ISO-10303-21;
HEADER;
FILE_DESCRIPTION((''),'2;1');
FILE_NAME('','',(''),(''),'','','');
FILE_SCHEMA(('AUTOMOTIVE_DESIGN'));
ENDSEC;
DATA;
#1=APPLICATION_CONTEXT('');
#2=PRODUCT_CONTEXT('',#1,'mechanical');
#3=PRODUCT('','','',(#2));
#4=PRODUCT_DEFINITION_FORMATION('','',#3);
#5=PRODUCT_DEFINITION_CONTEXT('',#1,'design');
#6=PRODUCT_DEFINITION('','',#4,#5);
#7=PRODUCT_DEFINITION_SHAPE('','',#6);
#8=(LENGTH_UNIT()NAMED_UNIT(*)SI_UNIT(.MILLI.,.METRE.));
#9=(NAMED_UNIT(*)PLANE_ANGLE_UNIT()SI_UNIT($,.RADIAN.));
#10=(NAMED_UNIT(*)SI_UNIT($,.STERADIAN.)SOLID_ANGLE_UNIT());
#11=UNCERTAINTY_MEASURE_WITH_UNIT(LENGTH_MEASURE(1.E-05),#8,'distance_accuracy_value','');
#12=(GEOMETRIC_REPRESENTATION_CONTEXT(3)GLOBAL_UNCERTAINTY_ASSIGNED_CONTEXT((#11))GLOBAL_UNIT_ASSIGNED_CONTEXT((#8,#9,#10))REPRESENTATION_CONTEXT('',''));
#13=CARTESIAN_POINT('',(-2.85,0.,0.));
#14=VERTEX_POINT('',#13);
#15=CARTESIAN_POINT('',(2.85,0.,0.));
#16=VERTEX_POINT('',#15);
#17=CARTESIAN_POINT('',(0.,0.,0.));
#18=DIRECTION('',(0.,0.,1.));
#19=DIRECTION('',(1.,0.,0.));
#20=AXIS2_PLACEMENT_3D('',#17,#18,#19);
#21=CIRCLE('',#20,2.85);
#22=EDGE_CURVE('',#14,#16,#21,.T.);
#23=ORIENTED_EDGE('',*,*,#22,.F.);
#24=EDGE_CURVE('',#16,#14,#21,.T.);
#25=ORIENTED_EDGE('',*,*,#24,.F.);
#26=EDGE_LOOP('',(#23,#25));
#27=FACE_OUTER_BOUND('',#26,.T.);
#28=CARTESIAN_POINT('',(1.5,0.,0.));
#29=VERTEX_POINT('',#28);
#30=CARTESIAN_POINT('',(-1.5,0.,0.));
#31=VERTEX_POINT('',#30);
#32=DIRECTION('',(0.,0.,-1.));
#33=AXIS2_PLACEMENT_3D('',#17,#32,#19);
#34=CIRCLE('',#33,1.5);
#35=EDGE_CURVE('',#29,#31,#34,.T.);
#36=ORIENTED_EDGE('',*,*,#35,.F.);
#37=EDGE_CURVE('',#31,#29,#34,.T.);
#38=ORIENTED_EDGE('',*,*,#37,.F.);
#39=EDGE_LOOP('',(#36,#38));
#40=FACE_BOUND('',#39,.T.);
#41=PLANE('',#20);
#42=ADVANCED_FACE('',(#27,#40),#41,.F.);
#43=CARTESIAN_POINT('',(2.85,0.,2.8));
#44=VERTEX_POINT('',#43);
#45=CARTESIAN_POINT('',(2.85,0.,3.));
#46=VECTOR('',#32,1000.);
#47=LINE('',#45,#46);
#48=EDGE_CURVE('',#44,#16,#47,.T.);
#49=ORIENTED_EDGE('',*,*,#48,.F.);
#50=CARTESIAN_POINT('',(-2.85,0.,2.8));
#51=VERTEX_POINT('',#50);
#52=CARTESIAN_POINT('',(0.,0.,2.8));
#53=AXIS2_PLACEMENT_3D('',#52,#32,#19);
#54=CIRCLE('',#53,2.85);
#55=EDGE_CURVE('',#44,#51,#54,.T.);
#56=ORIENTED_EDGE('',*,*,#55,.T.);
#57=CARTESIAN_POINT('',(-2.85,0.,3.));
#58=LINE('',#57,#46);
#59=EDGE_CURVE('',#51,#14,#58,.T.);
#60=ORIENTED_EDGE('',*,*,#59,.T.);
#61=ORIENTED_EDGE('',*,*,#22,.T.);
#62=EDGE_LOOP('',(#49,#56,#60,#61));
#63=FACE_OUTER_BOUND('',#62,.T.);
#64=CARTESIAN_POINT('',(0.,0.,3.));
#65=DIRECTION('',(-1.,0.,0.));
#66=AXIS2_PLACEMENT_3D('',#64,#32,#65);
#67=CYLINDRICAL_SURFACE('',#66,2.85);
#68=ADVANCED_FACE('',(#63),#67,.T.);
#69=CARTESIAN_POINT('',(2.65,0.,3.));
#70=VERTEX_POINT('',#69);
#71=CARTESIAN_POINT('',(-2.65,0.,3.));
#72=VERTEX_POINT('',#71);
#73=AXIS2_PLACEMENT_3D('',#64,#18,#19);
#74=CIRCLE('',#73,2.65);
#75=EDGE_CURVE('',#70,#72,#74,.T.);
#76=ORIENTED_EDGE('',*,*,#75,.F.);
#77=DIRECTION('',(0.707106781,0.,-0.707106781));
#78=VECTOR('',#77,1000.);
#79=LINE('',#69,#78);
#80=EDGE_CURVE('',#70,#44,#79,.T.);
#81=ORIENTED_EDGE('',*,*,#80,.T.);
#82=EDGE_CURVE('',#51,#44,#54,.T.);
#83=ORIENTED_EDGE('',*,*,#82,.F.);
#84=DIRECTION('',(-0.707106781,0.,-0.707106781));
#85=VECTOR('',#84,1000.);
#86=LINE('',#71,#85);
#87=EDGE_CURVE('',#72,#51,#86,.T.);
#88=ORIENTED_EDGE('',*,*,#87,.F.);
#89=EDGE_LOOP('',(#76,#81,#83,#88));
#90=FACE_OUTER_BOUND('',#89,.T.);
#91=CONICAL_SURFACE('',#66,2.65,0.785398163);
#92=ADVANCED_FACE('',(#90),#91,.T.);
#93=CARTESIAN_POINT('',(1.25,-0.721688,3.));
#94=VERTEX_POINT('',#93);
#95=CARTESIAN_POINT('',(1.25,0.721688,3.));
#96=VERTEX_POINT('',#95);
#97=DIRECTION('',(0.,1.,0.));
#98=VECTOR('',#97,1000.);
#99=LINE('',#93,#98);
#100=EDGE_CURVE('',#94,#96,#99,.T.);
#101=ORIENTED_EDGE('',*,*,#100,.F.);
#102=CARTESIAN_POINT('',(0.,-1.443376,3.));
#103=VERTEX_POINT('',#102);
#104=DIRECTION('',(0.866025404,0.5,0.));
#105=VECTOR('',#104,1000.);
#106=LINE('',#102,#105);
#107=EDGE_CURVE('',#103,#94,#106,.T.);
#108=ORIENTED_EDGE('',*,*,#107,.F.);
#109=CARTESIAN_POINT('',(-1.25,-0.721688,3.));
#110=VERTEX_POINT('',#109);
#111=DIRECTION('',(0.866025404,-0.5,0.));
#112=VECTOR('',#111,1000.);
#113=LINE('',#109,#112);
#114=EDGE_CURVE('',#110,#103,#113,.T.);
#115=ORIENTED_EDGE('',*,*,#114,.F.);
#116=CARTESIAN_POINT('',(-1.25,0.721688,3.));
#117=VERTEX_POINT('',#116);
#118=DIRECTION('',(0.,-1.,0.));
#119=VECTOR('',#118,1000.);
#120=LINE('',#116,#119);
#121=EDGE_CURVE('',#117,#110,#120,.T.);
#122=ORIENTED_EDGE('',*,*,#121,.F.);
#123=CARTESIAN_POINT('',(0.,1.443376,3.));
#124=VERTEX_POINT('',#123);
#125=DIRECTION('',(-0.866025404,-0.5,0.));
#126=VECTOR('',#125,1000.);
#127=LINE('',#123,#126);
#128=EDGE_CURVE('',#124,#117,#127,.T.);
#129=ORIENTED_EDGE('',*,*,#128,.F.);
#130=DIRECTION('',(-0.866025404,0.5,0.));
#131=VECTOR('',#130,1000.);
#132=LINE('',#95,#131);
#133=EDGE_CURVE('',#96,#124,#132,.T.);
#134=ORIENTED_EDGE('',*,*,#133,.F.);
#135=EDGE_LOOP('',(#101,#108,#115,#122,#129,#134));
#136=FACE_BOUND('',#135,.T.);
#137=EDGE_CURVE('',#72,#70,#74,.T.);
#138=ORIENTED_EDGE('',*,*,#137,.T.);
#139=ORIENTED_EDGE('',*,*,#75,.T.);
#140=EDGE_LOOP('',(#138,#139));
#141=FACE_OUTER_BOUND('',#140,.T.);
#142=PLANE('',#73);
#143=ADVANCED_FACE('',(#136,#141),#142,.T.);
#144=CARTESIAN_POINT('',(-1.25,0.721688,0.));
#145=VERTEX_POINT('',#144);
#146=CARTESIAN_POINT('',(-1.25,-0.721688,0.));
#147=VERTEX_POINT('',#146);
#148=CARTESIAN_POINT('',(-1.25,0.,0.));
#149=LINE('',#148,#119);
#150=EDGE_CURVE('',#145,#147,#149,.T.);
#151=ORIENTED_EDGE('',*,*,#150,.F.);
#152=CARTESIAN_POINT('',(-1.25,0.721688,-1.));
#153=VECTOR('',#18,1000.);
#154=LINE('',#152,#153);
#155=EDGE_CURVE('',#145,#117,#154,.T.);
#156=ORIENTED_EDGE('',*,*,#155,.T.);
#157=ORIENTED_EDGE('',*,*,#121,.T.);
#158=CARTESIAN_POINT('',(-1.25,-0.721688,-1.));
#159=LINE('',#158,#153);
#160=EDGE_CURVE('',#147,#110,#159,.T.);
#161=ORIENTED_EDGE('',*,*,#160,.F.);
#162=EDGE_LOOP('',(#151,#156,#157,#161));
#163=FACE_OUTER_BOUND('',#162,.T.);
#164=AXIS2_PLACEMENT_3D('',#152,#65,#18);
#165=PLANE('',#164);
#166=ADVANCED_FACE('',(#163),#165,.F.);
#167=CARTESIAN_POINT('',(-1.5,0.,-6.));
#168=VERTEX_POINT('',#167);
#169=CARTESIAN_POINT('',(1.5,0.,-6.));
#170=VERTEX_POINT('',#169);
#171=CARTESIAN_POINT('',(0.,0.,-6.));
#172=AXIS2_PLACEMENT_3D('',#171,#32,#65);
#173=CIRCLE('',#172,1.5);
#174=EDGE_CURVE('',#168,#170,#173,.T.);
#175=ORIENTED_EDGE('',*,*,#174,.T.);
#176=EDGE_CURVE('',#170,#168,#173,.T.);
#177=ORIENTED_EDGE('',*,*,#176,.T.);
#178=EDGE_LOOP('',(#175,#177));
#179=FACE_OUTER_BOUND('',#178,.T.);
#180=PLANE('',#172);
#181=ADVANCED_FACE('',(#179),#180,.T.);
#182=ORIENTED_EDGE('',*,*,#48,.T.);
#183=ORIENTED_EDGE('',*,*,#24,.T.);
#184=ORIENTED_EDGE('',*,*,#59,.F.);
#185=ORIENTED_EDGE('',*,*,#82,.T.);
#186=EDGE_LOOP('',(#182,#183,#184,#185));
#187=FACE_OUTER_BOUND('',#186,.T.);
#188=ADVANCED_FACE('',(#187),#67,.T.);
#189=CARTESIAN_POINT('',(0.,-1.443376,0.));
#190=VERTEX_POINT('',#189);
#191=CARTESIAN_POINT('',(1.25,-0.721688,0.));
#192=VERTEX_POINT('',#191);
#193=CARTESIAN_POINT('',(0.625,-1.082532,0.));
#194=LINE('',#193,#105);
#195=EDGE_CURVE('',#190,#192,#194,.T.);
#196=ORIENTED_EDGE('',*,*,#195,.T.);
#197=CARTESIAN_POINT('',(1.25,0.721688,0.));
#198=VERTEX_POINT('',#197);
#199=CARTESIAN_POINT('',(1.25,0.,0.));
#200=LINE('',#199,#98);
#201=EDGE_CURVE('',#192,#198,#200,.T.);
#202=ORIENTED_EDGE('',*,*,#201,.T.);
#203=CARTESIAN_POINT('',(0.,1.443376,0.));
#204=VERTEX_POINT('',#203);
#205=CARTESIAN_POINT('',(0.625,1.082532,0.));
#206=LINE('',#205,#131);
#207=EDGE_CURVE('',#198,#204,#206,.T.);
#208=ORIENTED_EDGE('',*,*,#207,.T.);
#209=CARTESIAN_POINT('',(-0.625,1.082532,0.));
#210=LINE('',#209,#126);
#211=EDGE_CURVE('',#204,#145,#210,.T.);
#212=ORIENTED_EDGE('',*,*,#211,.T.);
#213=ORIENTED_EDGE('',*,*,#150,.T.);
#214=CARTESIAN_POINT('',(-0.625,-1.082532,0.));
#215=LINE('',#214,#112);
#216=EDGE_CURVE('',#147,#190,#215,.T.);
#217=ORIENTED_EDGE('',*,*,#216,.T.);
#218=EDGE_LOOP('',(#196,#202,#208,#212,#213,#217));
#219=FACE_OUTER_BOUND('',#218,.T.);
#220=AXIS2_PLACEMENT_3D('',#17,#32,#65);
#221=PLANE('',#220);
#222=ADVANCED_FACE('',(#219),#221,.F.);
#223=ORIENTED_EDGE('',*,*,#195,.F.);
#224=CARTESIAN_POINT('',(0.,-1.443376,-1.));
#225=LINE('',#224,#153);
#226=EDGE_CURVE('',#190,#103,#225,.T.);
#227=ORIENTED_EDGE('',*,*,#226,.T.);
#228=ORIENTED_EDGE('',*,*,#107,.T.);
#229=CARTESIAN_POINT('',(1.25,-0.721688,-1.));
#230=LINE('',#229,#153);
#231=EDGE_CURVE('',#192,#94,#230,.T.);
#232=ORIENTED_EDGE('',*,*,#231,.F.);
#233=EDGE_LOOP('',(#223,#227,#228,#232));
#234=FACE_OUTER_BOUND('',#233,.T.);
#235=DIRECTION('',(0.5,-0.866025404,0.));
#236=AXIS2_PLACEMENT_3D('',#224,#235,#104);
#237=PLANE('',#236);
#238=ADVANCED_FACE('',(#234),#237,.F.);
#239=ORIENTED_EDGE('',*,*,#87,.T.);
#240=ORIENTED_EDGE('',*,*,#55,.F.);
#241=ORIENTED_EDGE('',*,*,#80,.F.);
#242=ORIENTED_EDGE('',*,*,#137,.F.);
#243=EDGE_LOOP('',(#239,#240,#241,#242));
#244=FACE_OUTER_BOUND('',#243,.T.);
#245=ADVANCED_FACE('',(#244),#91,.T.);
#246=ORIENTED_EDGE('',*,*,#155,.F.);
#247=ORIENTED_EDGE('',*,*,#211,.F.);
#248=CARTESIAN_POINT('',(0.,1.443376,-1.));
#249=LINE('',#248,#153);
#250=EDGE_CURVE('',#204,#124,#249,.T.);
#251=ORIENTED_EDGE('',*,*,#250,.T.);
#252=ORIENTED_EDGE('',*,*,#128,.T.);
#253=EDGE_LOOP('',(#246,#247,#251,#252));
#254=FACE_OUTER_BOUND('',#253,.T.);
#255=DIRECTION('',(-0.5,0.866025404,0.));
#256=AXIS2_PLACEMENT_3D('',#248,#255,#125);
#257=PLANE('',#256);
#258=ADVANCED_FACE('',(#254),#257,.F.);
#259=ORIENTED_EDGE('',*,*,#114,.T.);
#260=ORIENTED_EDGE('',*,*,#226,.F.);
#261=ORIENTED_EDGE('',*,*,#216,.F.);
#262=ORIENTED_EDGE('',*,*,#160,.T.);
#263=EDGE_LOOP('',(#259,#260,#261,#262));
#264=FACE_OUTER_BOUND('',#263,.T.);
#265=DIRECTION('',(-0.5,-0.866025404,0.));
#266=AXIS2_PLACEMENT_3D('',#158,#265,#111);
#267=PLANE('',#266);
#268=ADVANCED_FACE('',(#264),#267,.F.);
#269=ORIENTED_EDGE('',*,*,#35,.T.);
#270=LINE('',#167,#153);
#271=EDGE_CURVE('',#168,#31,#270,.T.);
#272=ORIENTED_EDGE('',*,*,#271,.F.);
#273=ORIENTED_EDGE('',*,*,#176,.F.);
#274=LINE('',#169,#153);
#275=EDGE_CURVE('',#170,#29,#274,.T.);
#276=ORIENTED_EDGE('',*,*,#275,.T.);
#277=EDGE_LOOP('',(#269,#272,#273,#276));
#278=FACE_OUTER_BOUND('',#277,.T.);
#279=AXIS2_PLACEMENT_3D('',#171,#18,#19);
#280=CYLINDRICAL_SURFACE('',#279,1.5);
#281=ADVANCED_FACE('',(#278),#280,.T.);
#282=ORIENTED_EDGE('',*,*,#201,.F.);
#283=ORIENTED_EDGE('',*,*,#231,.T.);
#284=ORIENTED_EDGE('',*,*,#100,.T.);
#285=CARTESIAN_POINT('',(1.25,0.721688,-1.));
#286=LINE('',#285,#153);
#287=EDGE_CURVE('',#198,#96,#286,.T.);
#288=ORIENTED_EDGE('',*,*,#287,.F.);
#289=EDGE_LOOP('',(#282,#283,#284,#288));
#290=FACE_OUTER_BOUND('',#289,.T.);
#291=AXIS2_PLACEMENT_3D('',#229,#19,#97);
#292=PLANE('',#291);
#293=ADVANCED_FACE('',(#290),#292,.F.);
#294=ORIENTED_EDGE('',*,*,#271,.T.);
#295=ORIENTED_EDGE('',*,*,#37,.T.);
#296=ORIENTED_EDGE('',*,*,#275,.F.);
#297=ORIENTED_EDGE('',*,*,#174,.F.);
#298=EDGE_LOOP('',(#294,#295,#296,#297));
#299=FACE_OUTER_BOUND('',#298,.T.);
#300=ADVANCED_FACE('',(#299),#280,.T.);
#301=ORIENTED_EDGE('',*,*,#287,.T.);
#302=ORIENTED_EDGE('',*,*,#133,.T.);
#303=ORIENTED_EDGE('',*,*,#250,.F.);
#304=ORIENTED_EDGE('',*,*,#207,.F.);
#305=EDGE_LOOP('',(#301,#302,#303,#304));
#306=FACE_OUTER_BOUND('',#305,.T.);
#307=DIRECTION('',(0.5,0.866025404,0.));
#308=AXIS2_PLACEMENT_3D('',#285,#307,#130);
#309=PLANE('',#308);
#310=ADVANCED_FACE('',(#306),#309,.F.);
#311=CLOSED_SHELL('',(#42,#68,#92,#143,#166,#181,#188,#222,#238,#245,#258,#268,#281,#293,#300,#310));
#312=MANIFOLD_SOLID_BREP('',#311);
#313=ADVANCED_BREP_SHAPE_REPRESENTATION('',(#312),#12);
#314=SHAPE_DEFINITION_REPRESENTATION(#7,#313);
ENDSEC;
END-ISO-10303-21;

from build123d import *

# Parameters (mm, degrees)
SKETCH_1_R          = 2.85
EXTRUDE_1_DEPTH     = 3
CUT_EXTRUDE_1_DEPTH = 4
CHAMFER_1_SIZE      = 0.2
SKETCH_3_R          = 1.5
EXTRUDE_2_DEPTH     = 6


with BuildPart() as part:
    # 草图1 → 凸台-拉伸1 (new body)
    with BuildSketch(Plane.XY):
        Circle(SKETCH_1_R)
    extrude(amount=EXTRUDE_1_DEPTH)

    # 草图2 → 切除-拉伸1 (cut)
    with BuildSketch(Plane.XY.offset(3)):
        Polygon((0, 1.443375673), (-1.25, 0.721687836), (-1.25, -0.721687836), (0, -1.443375673), (1.25, -0.721687836), (1.25, 0.721687836), align=None)
    extrude(amount=-CUT_EXTRUDE_1_DEPTH, mode=Mode.SUBTRACT)

    # 倒角1
    chamfer_1_edges = [part.edges().sort_by_distance(p)[0] for p in [
        (-2.85, 0, 3),
    ]]
    chamfer(chamfer_1_edges, length=CHAMFER_1_SIZE)

    # 草图3 → 凸台-拉伸2 (add)
    with BuildSketch(Plane(origin=(0, 0, 0), x_dir=(-1, 0, 0), z_dir=(0, 0, -1))):
        with Locations(Location((0, 0, 0), (0, 0, 180))):
            Circle(SKETCH_3_R)
    extrude(amount=EXTRUDE_2_DEPTH)


solid = part.part
